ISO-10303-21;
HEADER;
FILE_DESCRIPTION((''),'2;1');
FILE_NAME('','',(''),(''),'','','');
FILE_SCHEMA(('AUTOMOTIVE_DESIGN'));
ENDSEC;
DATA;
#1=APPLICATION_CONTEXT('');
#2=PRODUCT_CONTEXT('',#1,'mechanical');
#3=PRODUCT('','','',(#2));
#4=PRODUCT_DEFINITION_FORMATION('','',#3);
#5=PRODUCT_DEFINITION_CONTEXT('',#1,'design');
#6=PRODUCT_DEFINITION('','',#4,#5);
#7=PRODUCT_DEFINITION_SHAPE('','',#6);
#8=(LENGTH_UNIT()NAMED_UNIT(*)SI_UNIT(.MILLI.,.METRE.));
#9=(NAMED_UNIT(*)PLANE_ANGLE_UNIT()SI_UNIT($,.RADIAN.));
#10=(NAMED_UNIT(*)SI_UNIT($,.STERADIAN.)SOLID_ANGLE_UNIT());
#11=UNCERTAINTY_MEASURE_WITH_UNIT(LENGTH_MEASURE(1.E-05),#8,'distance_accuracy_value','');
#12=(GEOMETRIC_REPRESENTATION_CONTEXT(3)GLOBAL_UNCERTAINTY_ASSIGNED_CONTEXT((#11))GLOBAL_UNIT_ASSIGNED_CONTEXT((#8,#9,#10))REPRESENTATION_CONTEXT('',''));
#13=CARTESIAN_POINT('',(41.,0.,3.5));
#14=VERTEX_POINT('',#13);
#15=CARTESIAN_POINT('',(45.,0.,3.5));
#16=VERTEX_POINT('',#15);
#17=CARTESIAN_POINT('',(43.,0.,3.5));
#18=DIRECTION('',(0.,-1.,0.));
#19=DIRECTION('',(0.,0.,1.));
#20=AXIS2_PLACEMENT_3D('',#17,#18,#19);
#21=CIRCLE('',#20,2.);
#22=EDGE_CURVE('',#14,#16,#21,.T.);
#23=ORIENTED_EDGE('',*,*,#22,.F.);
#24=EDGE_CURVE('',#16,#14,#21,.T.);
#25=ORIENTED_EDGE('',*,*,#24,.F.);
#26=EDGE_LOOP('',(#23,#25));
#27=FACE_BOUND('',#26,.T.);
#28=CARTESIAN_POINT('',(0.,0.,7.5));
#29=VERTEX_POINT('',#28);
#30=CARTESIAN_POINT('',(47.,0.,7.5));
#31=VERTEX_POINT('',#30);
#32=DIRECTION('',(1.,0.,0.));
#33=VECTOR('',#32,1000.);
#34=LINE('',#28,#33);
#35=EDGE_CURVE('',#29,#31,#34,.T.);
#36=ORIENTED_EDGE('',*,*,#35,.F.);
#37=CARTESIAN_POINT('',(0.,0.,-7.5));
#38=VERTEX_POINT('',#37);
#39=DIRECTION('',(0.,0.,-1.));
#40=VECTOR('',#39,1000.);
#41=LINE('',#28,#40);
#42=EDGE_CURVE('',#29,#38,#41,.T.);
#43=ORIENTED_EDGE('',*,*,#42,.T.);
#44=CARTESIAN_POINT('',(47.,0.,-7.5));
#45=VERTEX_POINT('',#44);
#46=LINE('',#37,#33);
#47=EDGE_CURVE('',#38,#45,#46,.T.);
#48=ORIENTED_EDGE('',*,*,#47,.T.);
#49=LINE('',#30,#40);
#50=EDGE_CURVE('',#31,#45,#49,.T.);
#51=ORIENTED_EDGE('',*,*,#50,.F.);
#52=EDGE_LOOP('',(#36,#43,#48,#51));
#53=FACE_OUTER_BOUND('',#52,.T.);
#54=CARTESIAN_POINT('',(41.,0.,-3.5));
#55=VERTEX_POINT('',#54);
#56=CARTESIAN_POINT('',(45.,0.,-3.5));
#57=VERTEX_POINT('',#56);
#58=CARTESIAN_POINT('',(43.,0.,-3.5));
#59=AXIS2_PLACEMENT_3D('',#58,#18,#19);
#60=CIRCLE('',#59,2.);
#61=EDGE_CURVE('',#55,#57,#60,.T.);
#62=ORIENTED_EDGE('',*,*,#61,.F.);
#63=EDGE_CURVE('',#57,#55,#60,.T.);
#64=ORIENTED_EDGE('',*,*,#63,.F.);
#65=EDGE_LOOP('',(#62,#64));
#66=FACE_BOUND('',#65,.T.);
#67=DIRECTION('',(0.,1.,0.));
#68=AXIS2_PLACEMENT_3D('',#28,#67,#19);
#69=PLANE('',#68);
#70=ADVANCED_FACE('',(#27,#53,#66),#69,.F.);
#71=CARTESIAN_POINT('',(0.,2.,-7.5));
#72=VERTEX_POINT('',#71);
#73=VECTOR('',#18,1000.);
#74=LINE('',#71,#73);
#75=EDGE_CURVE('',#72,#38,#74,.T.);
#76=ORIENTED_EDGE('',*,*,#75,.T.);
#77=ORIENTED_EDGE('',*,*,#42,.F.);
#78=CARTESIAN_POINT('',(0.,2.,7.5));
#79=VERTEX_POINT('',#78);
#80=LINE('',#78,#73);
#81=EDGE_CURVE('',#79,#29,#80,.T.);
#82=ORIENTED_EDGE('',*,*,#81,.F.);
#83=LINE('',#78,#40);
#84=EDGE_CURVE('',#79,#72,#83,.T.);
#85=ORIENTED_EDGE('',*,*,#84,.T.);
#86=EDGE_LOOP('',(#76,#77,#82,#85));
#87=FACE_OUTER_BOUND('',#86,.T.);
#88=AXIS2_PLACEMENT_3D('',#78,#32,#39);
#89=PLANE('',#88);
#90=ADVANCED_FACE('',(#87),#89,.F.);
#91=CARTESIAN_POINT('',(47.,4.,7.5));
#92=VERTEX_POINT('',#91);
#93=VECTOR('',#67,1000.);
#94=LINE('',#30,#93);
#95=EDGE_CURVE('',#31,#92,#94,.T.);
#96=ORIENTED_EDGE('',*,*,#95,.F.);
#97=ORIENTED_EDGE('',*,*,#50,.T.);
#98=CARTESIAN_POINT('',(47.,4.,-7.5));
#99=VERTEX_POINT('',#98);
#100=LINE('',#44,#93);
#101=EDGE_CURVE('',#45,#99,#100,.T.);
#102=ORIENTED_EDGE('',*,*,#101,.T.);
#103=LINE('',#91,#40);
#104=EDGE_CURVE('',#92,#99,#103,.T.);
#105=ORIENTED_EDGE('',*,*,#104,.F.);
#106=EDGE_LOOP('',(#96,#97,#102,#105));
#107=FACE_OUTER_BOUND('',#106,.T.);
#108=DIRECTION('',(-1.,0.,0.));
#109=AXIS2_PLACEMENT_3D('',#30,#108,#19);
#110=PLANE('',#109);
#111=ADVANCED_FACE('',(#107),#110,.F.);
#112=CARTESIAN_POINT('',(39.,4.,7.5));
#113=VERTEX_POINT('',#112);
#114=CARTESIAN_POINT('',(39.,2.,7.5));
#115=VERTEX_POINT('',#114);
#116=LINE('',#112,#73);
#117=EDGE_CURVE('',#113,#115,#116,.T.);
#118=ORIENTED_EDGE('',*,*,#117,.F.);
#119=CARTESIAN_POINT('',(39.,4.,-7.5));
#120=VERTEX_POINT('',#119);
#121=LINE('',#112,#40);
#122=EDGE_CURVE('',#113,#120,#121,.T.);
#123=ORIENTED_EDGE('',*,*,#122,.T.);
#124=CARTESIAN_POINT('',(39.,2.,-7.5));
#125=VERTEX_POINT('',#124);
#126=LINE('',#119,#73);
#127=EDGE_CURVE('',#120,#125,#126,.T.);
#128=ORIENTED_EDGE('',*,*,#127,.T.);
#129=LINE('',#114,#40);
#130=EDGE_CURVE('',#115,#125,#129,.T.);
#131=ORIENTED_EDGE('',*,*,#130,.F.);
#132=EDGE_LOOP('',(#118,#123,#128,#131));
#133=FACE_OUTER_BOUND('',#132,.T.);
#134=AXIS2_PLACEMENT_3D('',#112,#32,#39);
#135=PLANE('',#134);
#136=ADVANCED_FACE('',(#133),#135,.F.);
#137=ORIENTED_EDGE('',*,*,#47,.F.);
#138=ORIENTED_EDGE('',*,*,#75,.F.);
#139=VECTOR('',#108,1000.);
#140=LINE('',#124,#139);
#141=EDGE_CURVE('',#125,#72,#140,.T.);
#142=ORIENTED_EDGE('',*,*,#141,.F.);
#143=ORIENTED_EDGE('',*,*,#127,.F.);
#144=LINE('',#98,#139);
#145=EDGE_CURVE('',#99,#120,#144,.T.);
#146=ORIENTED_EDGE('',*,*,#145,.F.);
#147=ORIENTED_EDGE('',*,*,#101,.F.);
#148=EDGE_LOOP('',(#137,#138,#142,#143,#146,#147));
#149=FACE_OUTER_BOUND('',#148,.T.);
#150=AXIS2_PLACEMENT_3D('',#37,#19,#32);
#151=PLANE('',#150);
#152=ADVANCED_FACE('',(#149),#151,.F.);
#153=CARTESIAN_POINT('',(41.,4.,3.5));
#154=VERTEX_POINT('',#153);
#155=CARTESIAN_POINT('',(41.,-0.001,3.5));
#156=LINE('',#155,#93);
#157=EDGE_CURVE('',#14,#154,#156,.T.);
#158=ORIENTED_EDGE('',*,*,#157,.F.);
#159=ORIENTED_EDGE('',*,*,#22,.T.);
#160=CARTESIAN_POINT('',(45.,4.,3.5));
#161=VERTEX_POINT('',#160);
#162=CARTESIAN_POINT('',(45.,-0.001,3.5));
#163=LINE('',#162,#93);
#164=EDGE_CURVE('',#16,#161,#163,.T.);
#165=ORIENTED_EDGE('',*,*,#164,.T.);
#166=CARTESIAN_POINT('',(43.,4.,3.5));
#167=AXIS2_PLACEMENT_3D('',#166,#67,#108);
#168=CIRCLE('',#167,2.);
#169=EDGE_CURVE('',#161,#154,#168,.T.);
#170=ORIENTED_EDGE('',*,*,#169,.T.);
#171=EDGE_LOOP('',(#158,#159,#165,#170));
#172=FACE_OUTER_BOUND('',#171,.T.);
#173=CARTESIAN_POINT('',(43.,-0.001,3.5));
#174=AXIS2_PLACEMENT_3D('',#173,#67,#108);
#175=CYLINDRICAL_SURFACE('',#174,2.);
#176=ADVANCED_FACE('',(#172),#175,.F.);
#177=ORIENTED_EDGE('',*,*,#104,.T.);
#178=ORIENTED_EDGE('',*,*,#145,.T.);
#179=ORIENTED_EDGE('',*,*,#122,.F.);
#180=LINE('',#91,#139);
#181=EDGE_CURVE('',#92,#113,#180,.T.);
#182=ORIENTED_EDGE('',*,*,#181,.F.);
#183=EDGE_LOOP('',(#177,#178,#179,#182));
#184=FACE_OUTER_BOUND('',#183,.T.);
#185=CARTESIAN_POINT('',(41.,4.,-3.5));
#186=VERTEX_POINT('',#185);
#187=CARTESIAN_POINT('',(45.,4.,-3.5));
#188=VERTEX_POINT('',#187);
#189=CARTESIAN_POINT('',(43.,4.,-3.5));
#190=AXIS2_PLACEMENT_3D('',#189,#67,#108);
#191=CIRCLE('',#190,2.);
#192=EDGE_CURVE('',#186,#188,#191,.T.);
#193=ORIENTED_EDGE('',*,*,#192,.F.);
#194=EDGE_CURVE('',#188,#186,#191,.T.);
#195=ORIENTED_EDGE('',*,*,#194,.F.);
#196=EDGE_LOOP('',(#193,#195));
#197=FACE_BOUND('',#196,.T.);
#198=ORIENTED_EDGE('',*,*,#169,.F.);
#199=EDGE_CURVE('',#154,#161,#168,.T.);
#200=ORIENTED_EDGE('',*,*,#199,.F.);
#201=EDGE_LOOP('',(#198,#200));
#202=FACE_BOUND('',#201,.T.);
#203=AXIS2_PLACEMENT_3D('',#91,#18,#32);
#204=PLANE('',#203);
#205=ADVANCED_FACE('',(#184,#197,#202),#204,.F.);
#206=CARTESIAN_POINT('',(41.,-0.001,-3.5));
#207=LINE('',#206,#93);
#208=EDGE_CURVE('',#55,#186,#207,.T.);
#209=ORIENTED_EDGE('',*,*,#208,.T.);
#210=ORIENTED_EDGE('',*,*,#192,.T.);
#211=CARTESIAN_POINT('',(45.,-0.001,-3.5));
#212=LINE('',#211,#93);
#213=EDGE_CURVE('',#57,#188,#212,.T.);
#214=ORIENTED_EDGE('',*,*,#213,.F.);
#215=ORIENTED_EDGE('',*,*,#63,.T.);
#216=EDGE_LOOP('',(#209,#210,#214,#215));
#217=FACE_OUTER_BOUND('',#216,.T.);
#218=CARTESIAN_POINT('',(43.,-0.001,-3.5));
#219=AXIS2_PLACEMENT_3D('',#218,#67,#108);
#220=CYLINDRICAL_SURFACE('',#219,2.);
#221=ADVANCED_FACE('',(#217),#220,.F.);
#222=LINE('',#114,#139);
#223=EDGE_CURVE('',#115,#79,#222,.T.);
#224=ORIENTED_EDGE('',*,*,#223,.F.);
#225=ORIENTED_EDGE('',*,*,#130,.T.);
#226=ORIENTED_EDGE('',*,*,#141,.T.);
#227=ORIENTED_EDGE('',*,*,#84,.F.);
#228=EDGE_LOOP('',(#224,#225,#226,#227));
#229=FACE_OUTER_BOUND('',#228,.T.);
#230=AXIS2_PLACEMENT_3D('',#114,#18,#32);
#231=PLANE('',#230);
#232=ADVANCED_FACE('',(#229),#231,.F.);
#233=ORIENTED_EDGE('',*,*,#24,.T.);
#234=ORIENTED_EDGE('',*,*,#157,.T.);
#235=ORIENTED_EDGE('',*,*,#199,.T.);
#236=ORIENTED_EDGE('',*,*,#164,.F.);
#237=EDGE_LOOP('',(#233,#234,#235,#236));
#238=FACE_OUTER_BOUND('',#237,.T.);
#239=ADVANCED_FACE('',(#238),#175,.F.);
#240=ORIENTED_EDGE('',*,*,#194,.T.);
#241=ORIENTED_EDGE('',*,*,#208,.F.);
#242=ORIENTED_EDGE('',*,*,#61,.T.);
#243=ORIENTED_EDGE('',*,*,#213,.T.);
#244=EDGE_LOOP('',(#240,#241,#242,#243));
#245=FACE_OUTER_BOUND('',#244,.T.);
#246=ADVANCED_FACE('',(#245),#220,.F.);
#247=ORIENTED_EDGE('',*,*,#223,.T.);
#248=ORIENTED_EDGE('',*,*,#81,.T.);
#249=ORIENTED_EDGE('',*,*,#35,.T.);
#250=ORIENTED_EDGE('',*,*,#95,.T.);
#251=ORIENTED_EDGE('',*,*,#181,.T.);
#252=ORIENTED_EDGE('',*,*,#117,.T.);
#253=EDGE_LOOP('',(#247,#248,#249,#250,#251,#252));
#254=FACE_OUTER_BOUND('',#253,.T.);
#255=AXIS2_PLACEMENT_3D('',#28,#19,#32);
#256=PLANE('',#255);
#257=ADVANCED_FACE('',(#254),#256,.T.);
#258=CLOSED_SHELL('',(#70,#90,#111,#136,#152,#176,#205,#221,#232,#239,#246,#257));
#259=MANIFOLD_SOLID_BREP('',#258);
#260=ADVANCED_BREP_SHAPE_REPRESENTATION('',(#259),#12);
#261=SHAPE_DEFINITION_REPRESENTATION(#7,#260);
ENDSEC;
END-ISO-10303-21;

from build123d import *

# Parameters (mm, degrees)
EXTRUDE_1_DEPTH     = 7.5
CUT_EXTRUDE_1_REACH = 49.762
SKETCH_2_R          = 2


with BuildPart() as part:
    # 草图1 → 凸台-拉伸1 (new, symmetric)
    with BuildSketch(Plane.XY):
        Polygon((0, 0), (47, 0), (47, 4), (39, 4), (39, 2), (0, 2), align=None)
    extrude(amount=EXTRUDE_1_DEPTH, both=True)

    # 草图2 → 切除-拉伸1 (cut, up to next)
    with BuildSketch(Plane(origin=(0, 4, 0), x_dir=(1, 0, 0), z_dir=(0, 1, 0)), mode=Mode.PRIVATE) as cut_extrude_1_sk1:
        with Locations(Location((43, 3.5, 0), (0, 0, 180))):
            Circle(SKETCH_2_R)
    cut_extrude_1_tool1 = extrude(cut_extrude_1_sk1.sketch, amount=-CUT_EXTRUDE_1_REACH, mode=Mode.PRIVATE) & part.part
    # 草图2 → 切除-拉伸1 (cut, up to next)
    with BuildSketch(Plane(origin=(0, 4, 0), x_dir=(1, 0, 0), z_dir=(0, 1, 0)), mode=Mode.PRIVATE) as cut_extrude_1_sk2:
        with Locations(Location((43, -3.5, 0), (0, 0, 180))):
            Circle(SKETCH_2_R)
    cut_extrude_1_tool2 = extrude(cut_extrude_1_sk2.sketch, amount=-CUT_EXTRUDE_1_REACH, mode=Mode.PRIVATE) & part.part
    add(cut_extrude_1_tool1.solids().sort_by_distance((43, 4, -3.5))[0], mode=Mode.SUBTRACT)
    add(cut_extrude_1_tool2.solids().sort_by_distance((43, 4, 3.5))[0], mode=Mode.SUBTRACT)


solid = part.part
